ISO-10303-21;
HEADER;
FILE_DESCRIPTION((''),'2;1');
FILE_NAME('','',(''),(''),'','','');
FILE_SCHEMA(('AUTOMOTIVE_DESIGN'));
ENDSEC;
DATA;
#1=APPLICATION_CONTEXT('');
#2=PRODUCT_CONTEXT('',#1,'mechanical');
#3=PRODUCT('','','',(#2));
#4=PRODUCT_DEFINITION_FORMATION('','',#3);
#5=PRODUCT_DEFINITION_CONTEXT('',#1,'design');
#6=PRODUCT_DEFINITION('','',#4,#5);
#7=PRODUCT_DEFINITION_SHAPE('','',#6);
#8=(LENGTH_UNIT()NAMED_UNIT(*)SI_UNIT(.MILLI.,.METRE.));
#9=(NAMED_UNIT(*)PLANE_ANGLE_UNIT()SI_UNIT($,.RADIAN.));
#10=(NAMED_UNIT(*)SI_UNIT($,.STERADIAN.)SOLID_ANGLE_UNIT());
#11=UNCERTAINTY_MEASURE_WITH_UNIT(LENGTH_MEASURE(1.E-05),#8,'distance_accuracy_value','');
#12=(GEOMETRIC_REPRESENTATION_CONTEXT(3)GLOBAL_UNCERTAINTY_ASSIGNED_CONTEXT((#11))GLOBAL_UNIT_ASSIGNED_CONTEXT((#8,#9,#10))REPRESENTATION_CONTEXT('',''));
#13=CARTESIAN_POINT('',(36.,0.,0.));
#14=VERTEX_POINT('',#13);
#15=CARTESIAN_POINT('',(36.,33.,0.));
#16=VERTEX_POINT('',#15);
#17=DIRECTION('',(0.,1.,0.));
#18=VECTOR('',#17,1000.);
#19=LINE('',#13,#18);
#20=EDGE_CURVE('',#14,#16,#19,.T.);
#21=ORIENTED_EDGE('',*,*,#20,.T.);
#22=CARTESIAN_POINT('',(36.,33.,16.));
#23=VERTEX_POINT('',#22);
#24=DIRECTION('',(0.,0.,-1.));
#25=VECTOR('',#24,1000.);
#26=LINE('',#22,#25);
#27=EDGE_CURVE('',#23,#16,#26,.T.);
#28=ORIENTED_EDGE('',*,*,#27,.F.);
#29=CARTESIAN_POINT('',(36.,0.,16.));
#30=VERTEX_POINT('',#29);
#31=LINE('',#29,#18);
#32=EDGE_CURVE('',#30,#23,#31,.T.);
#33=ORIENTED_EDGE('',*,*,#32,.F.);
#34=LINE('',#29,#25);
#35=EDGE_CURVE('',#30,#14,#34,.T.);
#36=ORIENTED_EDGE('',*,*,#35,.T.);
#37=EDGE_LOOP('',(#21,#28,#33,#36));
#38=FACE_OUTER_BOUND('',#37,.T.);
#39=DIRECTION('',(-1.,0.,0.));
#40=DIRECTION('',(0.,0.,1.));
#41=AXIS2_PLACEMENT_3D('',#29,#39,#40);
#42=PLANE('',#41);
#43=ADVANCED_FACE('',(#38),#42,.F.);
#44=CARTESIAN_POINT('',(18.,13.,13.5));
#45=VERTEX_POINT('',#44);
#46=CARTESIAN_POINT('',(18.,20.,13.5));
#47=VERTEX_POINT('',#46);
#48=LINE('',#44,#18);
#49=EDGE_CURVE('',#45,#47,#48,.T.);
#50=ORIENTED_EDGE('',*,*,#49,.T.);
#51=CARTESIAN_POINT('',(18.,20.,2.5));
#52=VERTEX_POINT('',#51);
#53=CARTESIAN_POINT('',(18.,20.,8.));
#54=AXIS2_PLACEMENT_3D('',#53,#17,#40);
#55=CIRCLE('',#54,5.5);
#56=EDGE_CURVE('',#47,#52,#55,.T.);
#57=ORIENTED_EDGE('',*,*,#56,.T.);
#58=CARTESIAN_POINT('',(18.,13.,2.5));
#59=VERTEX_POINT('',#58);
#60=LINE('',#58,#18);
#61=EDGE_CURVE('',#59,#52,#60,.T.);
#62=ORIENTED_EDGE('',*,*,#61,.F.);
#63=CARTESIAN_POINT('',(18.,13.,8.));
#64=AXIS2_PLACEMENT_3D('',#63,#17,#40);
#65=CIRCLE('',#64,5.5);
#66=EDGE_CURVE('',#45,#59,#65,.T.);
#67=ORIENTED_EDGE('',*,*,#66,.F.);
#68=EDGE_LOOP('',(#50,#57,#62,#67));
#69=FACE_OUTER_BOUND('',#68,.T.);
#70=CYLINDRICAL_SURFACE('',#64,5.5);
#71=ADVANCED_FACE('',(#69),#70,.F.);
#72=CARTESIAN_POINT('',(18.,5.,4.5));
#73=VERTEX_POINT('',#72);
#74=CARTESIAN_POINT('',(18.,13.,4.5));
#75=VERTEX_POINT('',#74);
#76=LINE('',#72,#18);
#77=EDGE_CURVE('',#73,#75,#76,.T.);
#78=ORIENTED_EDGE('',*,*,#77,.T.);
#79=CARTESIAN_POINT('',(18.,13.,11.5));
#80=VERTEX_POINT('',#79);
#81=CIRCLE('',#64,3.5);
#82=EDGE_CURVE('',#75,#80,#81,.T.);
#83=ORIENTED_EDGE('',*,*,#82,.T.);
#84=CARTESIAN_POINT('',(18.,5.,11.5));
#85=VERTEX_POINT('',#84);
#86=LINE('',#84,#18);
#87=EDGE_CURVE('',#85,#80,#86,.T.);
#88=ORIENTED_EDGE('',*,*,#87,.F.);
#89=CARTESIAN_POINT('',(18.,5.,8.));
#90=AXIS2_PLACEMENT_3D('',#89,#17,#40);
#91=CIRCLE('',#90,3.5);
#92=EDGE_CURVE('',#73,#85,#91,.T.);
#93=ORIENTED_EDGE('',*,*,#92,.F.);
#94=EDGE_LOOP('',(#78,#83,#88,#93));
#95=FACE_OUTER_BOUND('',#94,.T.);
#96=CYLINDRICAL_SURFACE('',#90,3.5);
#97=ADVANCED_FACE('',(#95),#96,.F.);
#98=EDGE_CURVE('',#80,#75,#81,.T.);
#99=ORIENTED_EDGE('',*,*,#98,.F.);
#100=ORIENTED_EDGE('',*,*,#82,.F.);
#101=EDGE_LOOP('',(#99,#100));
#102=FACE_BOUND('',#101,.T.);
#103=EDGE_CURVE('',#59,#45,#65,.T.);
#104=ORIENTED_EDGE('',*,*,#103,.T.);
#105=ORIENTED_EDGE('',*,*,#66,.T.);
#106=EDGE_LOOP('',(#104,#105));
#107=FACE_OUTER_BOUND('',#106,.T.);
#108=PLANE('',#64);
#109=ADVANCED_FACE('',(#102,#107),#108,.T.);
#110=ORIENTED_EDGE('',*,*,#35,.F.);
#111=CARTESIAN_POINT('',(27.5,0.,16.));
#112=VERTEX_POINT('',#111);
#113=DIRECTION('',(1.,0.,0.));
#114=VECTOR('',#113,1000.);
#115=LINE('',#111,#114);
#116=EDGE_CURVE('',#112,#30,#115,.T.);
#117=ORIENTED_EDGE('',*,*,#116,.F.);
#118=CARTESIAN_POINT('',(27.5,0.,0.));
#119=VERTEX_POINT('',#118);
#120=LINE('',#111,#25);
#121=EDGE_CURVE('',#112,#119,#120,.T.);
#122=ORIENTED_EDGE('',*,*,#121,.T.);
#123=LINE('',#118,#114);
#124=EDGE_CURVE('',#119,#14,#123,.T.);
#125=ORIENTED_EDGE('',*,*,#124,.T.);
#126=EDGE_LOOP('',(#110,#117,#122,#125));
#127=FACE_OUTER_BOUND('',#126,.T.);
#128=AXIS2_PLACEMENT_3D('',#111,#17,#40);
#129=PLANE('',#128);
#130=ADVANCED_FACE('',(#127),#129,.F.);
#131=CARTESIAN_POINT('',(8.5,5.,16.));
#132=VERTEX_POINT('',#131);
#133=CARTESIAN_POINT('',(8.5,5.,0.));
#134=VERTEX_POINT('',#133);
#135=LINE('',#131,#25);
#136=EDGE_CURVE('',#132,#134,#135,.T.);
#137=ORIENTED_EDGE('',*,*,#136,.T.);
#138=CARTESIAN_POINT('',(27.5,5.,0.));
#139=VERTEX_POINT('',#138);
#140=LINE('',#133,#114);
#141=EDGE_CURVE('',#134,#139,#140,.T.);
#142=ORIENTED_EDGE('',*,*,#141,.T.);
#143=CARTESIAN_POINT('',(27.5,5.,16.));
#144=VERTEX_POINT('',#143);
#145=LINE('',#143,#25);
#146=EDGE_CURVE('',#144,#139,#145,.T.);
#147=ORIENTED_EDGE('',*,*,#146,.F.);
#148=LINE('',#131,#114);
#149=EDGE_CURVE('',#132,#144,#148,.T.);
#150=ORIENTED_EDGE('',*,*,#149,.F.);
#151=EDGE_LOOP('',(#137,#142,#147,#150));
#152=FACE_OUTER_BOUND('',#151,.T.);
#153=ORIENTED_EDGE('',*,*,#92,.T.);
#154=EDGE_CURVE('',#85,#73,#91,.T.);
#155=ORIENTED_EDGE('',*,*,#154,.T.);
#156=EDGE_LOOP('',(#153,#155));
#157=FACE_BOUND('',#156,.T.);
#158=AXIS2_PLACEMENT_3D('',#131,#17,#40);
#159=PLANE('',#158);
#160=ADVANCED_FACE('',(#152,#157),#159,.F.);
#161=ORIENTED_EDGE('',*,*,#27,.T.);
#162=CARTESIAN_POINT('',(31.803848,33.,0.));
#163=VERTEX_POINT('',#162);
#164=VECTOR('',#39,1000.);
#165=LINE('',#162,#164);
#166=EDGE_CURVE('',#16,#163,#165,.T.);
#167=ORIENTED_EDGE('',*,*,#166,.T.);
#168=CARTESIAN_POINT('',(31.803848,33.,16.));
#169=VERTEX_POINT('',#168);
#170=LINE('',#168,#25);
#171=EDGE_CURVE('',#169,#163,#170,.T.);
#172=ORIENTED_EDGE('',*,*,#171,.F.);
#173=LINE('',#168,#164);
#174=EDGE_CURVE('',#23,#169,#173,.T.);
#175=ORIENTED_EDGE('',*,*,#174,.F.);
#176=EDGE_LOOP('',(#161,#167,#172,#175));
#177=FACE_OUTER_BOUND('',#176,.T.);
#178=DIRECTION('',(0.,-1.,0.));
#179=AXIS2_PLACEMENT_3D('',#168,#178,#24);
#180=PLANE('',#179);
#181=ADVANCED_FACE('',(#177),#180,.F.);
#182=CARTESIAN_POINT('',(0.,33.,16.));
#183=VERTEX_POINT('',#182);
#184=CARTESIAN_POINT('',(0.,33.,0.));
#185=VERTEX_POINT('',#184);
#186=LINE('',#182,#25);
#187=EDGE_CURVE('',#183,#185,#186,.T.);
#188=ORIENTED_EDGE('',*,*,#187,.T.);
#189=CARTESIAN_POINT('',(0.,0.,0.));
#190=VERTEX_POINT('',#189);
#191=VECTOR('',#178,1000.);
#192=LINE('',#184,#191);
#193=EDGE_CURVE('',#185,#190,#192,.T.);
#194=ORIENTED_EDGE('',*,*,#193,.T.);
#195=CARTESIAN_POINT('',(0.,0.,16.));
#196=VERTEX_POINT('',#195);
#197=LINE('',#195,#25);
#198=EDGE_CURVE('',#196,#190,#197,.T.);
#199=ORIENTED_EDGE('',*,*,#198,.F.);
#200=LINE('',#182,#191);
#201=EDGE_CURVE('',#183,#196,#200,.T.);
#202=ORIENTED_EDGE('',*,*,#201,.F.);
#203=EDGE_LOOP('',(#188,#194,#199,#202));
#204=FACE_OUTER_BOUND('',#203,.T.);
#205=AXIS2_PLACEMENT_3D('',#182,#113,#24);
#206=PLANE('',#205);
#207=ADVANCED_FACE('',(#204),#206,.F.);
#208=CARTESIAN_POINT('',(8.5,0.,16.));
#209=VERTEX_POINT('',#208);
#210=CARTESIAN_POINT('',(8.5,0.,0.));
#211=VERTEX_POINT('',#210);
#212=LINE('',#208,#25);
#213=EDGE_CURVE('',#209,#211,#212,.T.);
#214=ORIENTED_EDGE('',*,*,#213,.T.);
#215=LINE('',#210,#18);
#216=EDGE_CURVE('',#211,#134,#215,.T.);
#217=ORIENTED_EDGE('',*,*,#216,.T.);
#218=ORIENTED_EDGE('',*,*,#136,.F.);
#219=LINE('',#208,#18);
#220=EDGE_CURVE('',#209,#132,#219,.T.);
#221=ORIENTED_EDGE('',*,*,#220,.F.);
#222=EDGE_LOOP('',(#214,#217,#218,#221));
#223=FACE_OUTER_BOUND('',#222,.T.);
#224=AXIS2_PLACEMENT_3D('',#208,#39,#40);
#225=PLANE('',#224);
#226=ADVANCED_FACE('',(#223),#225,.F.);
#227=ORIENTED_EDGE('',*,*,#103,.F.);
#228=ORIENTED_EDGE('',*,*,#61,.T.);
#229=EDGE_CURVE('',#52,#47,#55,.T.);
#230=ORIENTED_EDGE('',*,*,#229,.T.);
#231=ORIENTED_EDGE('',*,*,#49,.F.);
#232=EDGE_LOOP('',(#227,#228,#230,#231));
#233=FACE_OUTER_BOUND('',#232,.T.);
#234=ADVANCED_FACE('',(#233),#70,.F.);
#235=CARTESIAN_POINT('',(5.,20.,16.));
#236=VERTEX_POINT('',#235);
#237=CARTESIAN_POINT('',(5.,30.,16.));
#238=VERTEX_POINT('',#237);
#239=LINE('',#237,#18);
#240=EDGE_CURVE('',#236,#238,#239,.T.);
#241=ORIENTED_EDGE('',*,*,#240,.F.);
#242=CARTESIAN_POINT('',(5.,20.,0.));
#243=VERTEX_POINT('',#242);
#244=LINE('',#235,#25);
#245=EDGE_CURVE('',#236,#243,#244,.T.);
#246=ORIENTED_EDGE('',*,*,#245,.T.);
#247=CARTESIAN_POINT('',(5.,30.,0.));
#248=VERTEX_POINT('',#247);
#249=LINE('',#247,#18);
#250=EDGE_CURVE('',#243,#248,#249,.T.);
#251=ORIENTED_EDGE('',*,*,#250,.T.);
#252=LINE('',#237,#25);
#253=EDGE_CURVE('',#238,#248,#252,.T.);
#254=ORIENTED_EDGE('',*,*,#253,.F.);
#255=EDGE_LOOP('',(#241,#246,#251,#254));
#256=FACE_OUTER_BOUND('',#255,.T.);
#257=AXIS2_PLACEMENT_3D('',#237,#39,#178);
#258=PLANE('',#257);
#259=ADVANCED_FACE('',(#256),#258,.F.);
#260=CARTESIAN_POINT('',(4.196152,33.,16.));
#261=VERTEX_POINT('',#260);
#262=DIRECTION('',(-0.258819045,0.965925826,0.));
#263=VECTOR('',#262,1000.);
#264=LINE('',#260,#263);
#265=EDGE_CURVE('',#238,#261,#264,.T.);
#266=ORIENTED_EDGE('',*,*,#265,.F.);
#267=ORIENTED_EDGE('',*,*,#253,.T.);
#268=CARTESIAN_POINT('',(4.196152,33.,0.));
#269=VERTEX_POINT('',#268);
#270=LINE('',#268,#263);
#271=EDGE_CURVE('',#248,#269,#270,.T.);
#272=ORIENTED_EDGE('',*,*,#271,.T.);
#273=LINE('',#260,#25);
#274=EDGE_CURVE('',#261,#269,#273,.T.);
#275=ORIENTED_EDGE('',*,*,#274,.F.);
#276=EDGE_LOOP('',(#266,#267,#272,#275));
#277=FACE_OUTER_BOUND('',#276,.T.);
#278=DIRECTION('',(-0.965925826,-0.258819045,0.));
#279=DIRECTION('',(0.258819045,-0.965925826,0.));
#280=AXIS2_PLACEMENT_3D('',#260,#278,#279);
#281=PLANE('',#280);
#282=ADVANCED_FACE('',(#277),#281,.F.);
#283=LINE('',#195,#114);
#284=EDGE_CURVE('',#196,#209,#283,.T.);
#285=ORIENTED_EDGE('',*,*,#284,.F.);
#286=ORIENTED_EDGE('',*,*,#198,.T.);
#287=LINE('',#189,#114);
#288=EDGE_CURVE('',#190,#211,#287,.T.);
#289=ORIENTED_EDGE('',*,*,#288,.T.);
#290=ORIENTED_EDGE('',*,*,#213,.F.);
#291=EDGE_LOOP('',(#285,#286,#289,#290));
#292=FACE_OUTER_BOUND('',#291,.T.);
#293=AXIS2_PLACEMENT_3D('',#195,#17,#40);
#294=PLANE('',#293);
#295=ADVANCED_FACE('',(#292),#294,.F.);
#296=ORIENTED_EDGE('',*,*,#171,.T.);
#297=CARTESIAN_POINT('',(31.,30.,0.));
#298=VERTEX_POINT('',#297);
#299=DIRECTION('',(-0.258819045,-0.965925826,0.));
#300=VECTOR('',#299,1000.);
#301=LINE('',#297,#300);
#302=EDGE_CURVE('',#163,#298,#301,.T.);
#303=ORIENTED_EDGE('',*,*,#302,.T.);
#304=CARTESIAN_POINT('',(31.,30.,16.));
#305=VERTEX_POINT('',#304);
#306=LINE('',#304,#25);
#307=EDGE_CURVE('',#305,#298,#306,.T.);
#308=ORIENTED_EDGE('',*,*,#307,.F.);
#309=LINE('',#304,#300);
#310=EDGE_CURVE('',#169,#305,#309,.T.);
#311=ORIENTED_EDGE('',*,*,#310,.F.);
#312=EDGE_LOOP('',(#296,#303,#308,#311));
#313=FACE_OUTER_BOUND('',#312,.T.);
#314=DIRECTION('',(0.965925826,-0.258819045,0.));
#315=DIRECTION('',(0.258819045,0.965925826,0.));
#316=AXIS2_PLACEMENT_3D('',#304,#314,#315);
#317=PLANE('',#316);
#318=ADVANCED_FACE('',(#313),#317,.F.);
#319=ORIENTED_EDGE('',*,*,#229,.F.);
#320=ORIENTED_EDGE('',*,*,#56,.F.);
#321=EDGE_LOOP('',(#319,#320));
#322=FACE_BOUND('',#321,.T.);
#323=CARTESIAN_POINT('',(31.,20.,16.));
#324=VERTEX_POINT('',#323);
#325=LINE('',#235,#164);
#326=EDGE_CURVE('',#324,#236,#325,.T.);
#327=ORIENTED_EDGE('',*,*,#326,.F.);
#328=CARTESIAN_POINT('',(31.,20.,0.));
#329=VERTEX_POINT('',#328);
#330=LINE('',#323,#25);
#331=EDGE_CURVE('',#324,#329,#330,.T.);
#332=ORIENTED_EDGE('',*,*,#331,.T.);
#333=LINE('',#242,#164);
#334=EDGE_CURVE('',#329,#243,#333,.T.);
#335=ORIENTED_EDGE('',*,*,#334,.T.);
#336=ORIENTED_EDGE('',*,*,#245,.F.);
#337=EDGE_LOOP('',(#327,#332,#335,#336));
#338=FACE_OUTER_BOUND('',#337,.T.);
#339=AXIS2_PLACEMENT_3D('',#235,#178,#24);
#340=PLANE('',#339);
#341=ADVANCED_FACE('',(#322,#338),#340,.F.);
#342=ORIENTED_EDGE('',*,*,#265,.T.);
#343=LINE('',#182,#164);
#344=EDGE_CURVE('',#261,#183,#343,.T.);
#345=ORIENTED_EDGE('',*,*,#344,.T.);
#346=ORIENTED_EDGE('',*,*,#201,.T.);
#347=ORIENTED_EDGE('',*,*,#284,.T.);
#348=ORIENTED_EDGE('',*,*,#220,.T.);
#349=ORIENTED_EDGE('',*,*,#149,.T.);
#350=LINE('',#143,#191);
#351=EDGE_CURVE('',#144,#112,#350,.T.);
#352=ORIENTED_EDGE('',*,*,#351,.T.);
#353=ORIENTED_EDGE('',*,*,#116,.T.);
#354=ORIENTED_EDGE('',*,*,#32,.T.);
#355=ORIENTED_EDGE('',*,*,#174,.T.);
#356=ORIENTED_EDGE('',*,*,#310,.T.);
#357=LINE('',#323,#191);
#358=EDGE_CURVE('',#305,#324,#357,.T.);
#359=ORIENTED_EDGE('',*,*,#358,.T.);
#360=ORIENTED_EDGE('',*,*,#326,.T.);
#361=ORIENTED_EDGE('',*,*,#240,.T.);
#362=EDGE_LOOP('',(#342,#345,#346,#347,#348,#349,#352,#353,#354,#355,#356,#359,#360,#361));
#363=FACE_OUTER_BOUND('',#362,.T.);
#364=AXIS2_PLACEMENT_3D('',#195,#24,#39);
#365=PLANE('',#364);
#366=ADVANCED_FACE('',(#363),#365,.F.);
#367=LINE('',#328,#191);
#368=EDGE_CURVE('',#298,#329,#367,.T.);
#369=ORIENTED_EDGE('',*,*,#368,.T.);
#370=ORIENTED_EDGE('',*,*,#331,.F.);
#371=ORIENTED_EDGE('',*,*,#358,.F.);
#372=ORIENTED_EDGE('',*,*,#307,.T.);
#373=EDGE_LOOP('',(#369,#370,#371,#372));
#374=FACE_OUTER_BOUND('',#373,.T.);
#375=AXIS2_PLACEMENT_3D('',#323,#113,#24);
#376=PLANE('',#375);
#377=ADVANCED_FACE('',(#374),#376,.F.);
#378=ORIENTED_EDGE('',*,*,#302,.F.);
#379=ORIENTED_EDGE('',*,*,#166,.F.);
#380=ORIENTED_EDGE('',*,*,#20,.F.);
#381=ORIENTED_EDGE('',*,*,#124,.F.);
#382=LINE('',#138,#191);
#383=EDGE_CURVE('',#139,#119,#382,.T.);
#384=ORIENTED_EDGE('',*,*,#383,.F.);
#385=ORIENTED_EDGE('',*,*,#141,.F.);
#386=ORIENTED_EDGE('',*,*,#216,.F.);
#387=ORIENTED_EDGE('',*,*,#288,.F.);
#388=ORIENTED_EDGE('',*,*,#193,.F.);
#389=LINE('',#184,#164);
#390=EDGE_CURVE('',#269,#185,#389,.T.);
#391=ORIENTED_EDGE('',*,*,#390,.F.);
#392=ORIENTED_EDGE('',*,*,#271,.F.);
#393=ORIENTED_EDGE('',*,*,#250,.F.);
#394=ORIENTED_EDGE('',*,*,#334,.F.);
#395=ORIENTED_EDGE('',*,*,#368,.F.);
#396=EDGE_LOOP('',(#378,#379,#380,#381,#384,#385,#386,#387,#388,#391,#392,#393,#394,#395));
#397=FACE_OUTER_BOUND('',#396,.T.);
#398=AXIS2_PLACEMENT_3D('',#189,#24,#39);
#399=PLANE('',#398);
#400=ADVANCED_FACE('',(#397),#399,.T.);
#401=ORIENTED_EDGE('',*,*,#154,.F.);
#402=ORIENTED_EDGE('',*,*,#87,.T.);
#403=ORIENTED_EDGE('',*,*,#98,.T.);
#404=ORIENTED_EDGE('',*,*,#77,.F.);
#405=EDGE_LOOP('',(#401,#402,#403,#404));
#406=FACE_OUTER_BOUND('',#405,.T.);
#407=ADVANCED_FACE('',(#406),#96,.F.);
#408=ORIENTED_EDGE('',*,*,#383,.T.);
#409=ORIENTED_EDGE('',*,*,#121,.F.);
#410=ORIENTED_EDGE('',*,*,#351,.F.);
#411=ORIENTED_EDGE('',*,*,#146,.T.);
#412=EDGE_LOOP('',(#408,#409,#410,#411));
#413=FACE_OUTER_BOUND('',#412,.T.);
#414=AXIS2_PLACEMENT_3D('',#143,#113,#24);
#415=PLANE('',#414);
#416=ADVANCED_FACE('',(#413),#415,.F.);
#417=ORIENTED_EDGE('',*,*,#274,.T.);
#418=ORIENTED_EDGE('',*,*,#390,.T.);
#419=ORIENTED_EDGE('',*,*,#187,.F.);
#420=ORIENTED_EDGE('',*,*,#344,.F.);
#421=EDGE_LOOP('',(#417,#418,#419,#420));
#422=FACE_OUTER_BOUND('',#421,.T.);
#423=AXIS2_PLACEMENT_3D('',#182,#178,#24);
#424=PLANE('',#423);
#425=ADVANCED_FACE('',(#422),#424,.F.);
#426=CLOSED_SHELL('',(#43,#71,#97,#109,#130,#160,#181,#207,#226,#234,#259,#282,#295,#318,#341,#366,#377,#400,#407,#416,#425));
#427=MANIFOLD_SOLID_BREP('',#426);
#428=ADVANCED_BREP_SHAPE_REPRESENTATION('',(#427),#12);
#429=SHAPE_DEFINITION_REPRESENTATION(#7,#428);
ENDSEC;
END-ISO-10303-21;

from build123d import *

# Parameters (mm, degrees)
BOSS_EXTRUDE1_DEPTH = 16
SKETCH2_R           = 5.5
CUT_EXTRUDE1_DEPTH  = 7
SKETCH3_R           = 3.5
CUT_EXTRUDE2_DEPTH  = 8


with BuildPart() as part:
    # Sketch1 → Boss-Extrude1 (new body)
    with BuildSketch(Plane.XY):
        Polygon((0, 33), (0, 0), (8.5, 0), (8.5, 5), (27.5, 5), (27.5, 0), (36, 0), (36, 33), (31.803847577, 33), (31, 30), (31, 20), (5, 20), (5, 30), (4.196152423, 33), align=None)
    extrude(amount=BOSS_EXTRUDE1_DEPTH)

    # Sketch2 → Cut-Extrude1 (cut)
    with BuildSketch(Plane(origin=(0, 20, 0), x_dir=(1, 0, 0), z_dir=(0, 1, 0))):
        with Locations(Location((18, -8, 0), (0, 0, 270))):
            Circle(SKETCH2_R)
    extrude(amount=-CUT_EXTRUDE1_DEPTH, mode=Mode.SUBTRACT)

    # Sketch3 → Cut-Extrude2 (cut)
    with BuildSketch(Plane(origin=(0, 13, 0), x_dir=(1, 0, 0), z_dir=(0, 1, 0))):
        with Locations(Location((18, -8, 0), (0, 0, 270))):
            Circle(SKETCH3_R)
    extrude(amount=-CUT_EXTRUDE2_DEPTH, mode=Mode.SUBTRACT)


solid = part.part
